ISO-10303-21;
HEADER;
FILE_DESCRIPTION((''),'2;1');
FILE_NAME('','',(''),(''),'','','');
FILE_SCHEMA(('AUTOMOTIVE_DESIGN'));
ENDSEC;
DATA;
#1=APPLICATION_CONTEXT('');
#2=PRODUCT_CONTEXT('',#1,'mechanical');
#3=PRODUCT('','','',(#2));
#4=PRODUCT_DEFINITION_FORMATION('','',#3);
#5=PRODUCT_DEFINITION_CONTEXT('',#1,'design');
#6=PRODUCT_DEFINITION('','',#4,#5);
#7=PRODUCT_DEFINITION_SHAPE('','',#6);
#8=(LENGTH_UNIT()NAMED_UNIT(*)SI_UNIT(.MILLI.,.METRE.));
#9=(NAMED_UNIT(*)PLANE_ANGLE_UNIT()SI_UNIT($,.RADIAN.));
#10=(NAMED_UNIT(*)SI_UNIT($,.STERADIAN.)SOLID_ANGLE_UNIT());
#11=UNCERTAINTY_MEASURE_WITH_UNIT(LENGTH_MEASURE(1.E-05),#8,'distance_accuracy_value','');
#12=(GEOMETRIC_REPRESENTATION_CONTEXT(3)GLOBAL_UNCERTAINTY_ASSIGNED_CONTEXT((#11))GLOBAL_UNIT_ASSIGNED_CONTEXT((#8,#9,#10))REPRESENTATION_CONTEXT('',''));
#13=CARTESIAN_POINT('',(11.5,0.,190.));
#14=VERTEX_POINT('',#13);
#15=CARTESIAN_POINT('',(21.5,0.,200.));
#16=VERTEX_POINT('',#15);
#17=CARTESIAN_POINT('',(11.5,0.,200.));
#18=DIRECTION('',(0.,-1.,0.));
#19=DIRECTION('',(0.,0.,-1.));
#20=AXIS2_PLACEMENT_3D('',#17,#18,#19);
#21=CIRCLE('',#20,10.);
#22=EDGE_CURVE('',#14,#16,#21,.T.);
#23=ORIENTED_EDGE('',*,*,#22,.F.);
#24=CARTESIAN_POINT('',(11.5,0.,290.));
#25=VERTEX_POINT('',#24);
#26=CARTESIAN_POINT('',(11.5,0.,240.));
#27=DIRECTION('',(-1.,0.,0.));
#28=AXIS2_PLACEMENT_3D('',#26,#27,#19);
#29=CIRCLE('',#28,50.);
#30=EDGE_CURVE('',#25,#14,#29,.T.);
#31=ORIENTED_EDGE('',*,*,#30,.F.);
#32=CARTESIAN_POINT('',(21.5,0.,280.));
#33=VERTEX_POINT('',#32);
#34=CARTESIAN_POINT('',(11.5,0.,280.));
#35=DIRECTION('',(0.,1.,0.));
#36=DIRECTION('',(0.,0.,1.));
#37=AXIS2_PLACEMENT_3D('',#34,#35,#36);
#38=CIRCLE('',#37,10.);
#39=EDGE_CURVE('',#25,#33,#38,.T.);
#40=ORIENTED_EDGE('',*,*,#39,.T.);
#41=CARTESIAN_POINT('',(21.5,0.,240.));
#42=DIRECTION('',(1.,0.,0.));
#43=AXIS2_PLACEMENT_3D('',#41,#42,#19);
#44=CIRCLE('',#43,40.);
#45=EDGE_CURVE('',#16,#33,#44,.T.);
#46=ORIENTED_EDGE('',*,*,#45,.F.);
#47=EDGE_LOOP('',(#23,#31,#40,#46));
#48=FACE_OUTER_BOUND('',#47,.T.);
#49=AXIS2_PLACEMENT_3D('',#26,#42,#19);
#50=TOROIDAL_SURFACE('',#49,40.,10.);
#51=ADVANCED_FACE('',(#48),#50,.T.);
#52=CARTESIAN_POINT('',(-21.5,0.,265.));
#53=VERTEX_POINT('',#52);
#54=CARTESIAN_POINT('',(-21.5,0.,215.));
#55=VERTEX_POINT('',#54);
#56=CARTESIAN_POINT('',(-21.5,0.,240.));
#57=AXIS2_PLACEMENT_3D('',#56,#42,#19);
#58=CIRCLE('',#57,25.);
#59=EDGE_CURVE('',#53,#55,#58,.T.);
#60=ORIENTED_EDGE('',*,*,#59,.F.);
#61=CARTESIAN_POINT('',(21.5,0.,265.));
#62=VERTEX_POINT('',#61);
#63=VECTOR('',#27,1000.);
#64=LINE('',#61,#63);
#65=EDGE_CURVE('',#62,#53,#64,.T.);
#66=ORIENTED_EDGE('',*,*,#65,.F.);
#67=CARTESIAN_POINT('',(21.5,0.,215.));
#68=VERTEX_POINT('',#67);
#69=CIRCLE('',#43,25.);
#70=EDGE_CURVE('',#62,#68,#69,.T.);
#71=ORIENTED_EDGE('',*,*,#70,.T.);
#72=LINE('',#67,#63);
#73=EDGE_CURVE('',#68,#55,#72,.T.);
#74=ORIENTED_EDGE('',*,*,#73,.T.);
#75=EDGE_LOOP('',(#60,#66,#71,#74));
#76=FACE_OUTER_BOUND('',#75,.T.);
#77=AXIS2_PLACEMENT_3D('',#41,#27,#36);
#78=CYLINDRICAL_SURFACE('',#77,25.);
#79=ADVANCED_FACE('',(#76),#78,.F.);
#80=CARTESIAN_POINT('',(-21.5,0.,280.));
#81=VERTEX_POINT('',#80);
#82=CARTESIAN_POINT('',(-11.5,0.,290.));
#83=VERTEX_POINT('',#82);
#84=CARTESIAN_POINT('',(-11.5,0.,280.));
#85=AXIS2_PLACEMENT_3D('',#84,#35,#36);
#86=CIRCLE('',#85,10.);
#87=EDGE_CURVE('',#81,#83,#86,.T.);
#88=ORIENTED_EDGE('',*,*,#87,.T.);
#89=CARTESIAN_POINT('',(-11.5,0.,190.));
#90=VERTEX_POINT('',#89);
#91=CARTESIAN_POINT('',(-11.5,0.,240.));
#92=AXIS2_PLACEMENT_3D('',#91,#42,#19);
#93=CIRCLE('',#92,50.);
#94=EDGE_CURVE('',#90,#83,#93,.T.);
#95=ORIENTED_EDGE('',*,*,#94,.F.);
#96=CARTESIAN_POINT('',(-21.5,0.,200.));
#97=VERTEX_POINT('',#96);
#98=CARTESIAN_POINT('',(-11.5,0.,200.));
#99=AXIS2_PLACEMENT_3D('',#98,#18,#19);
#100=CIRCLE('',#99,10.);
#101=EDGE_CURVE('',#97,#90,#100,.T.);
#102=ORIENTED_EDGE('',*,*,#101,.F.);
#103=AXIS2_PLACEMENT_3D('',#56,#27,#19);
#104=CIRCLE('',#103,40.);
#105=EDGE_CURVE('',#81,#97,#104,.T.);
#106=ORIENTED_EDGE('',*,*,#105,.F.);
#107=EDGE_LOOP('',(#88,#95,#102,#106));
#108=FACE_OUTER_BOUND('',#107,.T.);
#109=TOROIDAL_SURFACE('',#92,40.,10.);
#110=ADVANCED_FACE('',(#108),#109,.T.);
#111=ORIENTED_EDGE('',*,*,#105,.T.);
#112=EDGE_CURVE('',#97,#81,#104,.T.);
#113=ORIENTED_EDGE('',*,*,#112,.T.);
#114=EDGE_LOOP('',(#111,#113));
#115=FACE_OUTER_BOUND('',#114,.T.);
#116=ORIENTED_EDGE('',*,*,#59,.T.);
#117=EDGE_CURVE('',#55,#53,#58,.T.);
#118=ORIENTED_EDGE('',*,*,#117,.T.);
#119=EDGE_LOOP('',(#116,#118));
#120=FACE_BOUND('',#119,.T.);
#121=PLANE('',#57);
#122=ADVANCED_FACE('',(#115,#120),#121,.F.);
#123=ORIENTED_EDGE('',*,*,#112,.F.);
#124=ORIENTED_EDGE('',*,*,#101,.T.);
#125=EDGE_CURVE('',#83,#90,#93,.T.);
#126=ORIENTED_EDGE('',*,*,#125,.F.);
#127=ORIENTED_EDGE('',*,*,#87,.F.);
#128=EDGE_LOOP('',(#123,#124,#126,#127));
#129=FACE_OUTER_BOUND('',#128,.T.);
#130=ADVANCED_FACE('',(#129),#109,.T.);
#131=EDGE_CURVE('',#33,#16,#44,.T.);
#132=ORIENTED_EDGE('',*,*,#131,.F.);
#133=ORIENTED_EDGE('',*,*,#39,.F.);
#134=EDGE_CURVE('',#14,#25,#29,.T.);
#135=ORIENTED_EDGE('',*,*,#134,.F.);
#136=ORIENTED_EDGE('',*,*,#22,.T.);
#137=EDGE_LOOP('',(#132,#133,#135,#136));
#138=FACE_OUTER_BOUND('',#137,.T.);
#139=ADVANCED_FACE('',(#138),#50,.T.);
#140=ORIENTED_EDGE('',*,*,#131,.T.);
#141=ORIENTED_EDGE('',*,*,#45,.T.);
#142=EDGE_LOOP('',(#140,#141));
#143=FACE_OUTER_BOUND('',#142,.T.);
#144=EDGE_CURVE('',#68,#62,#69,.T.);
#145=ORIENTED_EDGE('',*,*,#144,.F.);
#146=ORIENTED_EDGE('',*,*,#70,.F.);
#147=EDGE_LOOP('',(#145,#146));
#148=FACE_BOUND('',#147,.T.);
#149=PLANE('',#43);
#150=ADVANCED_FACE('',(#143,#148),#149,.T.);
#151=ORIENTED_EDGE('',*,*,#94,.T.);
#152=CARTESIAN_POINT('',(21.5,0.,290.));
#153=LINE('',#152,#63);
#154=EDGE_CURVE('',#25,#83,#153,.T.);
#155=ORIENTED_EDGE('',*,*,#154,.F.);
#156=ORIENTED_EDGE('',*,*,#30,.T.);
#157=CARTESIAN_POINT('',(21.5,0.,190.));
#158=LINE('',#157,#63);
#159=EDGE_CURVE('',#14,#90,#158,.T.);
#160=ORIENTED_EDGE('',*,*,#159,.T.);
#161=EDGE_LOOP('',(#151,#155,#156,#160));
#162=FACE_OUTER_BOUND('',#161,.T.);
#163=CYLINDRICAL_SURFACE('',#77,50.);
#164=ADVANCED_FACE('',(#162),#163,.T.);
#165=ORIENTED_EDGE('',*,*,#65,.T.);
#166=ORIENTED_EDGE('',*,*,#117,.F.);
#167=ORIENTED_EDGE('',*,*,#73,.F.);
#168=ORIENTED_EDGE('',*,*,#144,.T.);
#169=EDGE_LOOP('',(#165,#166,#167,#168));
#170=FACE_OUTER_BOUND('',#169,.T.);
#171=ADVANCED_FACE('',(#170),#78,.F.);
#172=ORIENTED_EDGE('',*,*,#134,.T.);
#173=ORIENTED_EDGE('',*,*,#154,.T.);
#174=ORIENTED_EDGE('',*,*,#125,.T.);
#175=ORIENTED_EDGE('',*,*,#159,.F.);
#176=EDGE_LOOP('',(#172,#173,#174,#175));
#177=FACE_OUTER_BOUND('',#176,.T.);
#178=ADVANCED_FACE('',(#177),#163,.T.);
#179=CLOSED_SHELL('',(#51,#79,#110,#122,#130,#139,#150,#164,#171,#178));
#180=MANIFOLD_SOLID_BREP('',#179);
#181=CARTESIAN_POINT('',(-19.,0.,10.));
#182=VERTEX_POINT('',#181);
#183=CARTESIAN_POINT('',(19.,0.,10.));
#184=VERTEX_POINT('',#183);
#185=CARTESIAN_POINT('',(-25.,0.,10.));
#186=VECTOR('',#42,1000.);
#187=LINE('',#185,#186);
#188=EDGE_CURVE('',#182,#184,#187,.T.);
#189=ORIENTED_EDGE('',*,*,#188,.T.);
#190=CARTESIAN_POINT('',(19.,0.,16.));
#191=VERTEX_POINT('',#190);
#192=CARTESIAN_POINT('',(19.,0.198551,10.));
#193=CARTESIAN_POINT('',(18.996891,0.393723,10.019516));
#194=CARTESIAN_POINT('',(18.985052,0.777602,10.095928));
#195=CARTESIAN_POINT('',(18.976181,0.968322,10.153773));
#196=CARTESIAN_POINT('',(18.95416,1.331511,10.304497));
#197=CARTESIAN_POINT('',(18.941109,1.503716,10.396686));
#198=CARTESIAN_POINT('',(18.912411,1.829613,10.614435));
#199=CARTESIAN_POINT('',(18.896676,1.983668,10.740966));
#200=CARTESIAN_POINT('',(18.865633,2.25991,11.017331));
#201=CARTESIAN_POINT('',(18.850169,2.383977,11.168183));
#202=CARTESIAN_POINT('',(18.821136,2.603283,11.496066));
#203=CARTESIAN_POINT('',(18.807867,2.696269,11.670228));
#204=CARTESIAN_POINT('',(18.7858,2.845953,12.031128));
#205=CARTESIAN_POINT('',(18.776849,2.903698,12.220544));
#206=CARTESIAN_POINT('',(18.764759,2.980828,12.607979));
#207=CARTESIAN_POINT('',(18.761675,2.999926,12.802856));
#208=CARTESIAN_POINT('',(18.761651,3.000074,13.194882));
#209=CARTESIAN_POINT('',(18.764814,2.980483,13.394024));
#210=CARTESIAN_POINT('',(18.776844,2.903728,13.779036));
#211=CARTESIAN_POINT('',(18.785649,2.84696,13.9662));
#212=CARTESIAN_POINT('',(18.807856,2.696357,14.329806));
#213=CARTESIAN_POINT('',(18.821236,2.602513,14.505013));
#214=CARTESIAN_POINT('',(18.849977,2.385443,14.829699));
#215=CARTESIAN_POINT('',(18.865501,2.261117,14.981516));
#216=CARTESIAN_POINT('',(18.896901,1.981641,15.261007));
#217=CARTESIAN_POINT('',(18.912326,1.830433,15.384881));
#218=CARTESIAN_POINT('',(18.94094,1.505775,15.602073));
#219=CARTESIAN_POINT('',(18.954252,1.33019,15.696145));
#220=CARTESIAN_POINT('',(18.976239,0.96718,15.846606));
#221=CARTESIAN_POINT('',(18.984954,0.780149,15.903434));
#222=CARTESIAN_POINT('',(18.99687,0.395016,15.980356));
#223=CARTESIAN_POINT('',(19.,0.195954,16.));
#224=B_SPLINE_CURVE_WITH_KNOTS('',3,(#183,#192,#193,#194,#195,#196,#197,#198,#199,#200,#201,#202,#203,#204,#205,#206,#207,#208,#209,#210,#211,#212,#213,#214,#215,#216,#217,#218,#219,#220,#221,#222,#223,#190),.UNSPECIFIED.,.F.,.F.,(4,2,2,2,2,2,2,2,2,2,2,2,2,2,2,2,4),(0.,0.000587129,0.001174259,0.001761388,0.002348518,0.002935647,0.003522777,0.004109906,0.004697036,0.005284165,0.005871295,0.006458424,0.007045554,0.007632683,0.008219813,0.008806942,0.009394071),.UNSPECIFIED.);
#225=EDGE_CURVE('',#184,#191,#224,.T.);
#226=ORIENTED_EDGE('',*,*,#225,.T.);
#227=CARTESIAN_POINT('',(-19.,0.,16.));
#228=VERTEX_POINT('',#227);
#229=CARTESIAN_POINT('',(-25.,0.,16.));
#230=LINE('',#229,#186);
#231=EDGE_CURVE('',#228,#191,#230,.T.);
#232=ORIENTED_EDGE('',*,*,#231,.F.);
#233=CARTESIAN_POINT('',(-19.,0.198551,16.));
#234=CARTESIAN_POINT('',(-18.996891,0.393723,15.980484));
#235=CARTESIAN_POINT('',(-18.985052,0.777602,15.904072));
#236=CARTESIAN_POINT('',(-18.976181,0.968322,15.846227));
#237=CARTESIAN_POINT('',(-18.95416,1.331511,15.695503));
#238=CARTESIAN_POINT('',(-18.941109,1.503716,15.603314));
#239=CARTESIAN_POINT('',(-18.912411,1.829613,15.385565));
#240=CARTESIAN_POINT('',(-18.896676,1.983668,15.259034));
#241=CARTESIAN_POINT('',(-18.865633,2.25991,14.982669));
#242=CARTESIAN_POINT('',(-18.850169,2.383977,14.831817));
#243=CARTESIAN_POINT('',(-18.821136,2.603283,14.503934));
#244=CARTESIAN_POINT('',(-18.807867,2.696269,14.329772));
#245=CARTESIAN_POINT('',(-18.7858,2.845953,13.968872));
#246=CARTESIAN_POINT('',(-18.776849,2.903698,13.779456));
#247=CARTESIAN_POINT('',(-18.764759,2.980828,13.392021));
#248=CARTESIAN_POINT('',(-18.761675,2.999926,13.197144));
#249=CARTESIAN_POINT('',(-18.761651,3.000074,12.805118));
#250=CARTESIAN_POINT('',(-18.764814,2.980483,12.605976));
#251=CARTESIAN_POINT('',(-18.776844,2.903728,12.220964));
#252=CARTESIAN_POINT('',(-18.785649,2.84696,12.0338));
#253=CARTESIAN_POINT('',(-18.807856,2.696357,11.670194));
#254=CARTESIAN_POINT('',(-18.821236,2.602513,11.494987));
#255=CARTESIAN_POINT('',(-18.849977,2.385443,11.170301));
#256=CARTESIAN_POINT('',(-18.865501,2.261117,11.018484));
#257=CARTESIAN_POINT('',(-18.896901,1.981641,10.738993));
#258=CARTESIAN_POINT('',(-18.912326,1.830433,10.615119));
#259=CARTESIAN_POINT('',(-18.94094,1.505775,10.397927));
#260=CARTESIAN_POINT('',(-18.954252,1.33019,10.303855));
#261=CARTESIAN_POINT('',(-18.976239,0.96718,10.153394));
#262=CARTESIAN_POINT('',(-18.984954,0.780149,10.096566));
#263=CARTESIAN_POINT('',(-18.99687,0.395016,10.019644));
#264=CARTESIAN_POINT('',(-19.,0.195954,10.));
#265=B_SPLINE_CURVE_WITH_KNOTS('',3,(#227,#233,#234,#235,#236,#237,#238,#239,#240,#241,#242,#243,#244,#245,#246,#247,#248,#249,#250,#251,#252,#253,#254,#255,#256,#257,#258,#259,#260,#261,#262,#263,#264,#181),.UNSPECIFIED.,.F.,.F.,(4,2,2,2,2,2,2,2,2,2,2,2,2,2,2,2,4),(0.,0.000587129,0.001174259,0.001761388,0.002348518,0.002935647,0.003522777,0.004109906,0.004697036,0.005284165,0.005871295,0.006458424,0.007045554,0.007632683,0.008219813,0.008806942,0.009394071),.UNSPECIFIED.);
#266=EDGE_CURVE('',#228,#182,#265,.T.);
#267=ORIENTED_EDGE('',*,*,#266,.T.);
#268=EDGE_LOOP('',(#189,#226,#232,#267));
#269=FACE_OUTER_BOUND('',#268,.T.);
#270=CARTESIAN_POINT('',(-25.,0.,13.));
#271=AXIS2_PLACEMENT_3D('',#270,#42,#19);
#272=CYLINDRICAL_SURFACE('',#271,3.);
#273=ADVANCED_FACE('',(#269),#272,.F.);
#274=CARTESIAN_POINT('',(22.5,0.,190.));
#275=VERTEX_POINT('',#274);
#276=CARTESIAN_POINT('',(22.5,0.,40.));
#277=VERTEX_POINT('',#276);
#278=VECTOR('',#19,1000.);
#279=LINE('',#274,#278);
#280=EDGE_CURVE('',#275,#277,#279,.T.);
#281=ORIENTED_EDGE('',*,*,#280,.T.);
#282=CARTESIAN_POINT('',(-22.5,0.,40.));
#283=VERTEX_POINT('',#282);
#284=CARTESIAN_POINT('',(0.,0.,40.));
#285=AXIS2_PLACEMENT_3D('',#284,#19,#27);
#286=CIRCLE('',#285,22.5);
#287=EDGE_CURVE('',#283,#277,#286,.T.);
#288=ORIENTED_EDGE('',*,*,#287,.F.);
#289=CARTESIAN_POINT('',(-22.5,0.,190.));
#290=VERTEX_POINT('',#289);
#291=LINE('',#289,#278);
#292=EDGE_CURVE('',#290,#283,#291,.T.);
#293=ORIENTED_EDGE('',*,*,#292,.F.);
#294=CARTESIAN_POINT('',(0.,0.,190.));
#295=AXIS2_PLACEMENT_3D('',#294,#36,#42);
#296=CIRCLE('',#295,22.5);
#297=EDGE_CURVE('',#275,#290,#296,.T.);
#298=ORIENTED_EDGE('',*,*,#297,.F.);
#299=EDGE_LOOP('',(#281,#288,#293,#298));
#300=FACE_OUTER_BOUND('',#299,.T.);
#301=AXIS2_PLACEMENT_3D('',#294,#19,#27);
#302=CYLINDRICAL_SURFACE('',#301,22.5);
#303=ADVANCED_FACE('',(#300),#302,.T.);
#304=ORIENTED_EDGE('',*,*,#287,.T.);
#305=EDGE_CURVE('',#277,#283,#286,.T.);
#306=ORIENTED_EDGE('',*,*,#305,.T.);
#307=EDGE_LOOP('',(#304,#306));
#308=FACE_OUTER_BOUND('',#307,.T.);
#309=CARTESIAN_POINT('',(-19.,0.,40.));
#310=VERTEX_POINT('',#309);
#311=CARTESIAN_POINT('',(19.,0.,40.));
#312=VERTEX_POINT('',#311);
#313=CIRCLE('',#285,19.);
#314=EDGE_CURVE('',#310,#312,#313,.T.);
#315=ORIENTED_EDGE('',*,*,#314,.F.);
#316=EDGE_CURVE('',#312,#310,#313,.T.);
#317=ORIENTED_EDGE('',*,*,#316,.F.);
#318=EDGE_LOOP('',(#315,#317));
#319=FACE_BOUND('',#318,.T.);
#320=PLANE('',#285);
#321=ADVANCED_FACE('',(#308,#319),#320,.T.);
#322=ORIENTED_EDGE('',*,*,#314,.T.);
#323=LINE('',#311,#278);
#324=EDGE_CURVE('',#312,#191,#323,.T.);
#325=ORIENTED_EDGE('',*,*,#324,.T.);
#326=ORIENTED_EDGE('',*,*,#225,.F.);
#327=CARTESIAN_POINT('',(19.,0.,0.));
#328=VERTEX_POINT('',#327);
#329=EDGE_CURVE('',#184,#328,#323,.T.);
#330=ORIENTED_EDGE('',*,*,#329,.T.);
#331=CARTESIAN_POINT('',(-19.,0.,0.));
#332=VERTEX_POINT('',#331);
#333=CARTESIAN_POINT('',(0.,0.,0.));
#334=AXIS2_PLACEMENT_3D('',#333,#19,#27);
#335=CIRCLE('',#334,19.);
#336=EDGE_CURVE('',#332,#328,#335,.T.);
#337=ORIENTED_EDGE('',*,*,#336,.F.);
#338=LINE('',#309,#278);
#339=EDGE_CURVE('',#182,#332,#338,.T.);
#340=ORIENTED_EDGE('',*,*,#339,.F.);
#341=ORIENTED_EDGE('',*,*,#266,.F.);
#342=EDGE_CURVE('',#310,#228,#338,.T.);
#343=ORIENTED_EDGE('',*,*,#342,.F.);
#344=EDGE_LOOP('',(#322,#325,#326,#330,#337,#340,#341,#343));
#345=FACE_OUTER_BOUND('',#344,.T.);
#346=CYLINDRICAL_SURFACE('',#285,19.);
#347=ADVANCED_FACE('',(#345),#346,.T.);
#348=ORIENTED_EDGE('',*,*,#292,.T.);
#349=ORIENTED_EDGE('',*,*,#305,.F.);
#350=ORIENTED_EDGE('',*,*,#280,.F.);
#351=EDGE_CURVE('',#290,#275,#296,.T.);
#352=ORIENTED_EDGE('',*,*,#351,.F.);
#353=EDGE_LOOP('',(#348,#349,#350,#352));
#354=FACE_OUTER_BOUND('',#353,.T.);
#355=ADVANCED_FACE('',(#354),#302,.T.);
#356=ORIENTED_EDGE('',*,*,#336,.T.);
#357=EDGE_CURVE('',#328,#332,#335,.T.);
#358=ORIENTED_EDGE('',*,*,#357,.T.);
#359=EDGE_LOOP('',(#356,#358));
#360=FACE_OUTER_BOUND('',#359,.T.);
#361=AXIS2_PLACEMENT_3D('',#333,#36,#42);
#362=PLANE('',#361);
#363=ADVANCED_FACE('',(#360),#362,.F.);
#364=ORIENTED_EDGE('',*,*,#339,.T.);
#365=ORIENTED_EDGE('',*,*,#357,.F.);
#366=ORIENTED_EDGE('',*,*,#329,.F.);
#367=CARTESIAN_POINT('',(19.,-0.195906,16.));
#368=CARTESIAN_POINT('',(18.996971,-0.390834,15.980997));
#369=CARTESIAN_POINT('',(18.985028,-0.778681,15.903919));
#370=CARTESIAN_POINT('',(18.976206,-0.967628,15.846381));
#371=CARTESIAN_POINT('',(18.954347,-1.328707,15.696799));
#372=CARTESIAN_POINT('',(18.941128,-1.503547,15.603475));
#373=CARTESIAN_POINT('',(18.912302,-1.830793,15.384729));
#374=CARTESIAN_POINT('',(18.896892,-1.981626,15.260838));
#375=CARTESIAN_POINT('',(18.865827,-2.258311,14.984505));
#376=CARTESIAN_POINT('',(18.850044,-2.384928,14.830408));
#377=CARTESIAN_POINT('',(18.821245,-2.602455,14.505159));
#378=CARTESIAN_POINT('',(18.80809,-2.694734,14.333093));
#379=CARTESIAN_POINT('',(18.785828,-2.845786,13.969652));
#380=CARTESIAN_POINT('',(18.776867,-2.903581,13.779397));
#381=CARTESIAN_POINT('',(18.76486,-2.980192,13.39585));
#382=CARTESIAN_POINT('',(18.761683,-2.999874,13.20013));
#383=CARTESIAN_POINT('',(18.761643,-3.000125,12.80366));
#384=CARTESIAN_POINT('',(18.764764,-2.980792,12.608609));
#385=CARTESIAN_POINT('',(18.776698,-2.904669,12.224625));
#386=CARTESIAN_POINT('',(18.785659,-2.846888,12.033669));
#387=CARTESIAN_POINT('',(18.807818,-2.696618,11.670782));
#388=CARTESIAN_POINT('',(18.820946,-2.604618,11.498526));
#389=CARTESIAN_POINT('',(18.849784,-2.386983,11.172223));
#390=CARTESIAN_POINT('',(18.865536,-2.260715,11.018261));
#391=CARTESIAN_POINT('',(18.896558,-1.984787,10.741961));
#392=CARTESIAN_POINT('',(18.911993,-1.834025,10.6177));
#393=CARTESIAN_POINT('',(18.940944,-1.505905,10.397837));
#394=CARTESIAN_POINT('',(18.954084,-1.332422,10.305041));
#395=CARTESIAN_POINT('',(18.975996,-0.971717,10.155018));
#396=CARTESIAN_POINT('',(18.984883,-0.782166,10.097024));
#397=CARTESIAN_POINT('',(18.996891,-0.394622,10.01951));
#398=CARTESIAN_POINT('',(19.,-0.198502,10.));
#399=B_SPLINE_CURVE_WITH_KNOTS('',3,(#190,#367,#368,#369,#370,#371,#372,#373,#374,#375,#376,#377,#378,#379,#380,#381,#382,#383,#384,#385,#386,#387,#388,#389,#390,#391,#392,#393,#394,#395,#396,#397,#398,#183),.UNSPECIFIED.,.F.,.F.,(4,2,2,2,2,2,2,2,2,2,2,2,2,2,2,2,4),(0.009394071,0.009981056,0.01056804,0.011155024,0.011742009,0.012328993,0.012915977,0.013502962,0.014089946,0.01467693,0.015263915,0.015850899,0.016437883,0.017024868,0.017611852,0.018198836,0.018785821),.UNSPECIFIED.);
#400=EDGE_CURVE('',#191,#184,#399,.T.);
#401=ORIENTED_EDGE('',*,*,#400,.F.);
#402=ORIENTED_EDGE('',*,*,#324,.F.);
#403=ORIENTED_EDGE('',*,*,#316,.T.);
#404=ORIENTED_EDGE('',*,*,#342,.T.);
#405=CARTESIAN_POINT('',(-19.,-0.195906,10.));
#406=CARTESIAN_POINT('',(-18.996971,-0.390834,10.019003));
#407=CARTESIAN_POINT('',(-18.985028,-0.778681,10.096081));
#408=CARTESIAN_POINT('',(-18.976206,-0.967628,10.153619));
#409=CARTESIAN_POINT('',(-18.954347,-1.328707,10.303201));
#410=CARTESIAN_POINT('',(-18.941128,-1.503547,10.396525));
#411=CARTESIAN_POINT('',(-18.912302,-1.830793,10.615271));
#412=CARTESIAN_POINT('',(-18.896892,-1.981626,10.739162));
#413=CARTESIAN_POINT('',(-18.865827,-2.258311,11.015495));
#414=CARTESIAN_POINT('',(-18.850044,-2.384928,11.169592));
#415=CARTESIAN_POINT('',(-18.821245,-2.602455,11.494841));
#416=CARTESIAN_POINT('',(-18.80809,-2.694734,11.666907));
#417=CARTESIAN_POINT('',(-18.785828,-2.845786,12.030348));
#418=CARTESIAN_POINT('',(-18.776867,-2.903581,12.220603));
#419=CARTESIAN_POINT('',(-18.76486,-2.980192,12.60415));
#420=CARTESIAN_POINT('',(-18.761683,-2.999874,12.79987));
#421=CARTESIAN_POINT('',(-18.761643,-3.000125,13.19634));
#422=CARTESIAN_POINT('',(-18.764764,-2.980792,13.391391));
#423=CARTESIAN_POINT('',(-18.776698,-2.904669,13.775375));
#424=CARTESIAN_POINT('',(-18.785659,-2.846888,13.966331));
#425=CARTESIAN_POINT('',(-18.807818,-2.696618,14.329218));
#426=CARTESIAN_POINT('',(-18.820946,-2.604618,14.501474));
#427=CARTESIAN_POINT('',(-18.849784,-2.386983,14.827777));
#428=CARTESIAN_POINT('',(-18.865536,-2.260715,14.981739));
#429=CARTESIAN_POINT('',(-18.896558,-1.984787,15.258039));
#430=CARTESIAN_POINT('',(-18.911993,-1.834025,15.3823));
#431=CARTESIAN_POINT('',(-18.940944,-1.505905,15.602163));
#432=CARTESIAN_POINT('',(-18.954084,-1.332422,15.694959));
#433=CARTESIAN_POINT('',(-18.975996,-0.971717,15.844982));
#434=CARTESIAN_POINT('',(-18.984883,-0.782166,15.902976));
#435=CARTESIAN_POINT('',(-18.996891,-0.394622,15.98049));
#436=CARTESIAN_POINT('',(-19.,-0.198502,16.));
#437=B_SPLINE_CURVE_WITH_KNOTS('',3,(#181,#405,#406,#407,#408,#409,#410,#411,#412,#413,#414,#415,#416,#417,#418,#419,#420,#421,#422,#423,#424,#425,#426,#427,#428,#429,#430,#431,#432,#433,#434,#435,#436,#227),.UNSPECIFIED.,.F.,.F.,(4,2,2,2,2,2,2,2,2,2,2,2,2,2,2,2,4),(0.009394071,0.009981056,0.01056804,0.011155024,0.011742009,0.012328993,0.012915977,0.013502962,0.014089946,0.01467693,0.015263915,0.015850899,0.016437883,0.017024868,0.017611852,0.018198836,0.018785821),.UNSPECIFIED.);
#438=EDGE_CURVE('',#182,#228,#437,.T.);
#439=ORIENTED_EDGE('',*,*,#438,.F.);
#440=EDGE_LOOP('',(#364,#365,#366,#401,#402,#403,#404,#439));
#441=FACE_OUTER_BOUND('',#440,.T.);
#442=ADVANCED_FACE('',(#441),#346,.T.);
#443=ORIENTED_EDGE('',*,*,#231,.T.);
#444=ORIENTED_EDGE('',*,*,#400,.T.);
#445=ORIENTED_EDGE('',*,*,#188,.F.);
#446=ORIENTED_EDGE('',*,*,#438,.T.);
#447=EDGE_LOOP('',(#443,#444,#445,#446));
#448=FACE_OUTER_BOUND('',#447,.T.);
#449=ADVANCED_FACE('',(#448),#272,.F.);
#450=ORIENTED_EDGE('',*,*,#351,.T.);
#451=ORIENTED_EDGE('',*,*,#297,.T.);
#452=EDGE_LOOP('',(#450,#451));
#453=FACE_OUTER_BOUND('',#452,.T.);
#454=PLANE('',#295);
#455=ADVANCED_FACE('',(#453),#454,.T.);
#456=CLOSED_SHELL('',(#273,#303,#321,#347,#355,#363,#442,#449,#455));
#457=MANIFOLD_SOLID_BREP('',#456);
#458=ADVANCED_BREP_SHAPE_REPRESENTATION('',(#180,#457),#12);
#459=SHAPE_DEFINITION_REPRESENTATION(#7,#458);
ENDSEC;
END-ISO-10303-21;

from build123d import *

# Parameters (mm, degrees)
SKETCH_1_R          = 22.5
EXTRUDE_1_DEPTH     = 190
SKETCH_2_R          = 50
SKETCH_2_R_2        = 25
EXTRUDE_2_DEPTH     = 21.5
FILLET_1_R          = 10
SKETCH_3_R          = 22.5
SKETCH_3_R_2        = 19
CUT_EXTRUDE_1_DEPTH = 40
SKETCH_4_R          = 3
CUT_EXTRUDE_2_DEPTH = 25


with BuildPart() as part:
    # 草图1 → 凸台-拉伸1 (new body)
    with BuildSketch(Plane.XY):
        Circle(SKETCH_1_R)
    extrude(amount=EXTRUDE_1_DEPTH)

    # 草图3 → 切除-拉伸1 (cut)
    with BuildSketch(Plane(origin=(0, 0, 0), x_dir=(-1, 0, 0), z_dir=(0, 0, -1))):
        Circle(SKETCH_3_R)
        Circle(SKETCH_3_R_2, mode=Mode.SUBTRACT)
    extrude(amount=-CUT_EXTRUDE_1_DEPTH, mode=Mode.SUBTRACT)

    # 草图4 → 切除-拉伸2 (cut, symmetric)
    with BuildSketch(Plane(origin=(0, 0, 0), x_dir=(0, 0, -1), z_dir=(1, 0, 0))):
        with Locations((-13, 0)):
            Circle(SKETCH_4_R)
    extrude(amount=CUT_EXTRUDE_2_DEPTH, both=True, mode=Mode.SUBTRACT)


with BuildPart() as body_2:
    # 草图2 → 凸台-拉伸2 (new, symmetric)
    with BuildSketch(Plane(origin=(0, 0, 0), x_dir=(0, 0, -1), z_dir=(1, 0, 0))):
        with Locations((-240, 0)):
            Circle(SKETCH_2_R)
        with Locations((-240, 0)):
            Circle(SKETCH_2_R_2, mode=Mode.SUBTRACT)
    extrude(amount=EXTRUDE_2_DEPTH, both=True)

    # 圆角1
    fillet_1_edges = [body_2.edges().sort_by_distance(p)[0] for p in [
        (-21.5, 0, 290),
        (21.5, 0, 290),
    ]]
    fillet(fillet_1_edges, radius=FILLET_1_R)


solid = Compound([part.part, body_2.part])
